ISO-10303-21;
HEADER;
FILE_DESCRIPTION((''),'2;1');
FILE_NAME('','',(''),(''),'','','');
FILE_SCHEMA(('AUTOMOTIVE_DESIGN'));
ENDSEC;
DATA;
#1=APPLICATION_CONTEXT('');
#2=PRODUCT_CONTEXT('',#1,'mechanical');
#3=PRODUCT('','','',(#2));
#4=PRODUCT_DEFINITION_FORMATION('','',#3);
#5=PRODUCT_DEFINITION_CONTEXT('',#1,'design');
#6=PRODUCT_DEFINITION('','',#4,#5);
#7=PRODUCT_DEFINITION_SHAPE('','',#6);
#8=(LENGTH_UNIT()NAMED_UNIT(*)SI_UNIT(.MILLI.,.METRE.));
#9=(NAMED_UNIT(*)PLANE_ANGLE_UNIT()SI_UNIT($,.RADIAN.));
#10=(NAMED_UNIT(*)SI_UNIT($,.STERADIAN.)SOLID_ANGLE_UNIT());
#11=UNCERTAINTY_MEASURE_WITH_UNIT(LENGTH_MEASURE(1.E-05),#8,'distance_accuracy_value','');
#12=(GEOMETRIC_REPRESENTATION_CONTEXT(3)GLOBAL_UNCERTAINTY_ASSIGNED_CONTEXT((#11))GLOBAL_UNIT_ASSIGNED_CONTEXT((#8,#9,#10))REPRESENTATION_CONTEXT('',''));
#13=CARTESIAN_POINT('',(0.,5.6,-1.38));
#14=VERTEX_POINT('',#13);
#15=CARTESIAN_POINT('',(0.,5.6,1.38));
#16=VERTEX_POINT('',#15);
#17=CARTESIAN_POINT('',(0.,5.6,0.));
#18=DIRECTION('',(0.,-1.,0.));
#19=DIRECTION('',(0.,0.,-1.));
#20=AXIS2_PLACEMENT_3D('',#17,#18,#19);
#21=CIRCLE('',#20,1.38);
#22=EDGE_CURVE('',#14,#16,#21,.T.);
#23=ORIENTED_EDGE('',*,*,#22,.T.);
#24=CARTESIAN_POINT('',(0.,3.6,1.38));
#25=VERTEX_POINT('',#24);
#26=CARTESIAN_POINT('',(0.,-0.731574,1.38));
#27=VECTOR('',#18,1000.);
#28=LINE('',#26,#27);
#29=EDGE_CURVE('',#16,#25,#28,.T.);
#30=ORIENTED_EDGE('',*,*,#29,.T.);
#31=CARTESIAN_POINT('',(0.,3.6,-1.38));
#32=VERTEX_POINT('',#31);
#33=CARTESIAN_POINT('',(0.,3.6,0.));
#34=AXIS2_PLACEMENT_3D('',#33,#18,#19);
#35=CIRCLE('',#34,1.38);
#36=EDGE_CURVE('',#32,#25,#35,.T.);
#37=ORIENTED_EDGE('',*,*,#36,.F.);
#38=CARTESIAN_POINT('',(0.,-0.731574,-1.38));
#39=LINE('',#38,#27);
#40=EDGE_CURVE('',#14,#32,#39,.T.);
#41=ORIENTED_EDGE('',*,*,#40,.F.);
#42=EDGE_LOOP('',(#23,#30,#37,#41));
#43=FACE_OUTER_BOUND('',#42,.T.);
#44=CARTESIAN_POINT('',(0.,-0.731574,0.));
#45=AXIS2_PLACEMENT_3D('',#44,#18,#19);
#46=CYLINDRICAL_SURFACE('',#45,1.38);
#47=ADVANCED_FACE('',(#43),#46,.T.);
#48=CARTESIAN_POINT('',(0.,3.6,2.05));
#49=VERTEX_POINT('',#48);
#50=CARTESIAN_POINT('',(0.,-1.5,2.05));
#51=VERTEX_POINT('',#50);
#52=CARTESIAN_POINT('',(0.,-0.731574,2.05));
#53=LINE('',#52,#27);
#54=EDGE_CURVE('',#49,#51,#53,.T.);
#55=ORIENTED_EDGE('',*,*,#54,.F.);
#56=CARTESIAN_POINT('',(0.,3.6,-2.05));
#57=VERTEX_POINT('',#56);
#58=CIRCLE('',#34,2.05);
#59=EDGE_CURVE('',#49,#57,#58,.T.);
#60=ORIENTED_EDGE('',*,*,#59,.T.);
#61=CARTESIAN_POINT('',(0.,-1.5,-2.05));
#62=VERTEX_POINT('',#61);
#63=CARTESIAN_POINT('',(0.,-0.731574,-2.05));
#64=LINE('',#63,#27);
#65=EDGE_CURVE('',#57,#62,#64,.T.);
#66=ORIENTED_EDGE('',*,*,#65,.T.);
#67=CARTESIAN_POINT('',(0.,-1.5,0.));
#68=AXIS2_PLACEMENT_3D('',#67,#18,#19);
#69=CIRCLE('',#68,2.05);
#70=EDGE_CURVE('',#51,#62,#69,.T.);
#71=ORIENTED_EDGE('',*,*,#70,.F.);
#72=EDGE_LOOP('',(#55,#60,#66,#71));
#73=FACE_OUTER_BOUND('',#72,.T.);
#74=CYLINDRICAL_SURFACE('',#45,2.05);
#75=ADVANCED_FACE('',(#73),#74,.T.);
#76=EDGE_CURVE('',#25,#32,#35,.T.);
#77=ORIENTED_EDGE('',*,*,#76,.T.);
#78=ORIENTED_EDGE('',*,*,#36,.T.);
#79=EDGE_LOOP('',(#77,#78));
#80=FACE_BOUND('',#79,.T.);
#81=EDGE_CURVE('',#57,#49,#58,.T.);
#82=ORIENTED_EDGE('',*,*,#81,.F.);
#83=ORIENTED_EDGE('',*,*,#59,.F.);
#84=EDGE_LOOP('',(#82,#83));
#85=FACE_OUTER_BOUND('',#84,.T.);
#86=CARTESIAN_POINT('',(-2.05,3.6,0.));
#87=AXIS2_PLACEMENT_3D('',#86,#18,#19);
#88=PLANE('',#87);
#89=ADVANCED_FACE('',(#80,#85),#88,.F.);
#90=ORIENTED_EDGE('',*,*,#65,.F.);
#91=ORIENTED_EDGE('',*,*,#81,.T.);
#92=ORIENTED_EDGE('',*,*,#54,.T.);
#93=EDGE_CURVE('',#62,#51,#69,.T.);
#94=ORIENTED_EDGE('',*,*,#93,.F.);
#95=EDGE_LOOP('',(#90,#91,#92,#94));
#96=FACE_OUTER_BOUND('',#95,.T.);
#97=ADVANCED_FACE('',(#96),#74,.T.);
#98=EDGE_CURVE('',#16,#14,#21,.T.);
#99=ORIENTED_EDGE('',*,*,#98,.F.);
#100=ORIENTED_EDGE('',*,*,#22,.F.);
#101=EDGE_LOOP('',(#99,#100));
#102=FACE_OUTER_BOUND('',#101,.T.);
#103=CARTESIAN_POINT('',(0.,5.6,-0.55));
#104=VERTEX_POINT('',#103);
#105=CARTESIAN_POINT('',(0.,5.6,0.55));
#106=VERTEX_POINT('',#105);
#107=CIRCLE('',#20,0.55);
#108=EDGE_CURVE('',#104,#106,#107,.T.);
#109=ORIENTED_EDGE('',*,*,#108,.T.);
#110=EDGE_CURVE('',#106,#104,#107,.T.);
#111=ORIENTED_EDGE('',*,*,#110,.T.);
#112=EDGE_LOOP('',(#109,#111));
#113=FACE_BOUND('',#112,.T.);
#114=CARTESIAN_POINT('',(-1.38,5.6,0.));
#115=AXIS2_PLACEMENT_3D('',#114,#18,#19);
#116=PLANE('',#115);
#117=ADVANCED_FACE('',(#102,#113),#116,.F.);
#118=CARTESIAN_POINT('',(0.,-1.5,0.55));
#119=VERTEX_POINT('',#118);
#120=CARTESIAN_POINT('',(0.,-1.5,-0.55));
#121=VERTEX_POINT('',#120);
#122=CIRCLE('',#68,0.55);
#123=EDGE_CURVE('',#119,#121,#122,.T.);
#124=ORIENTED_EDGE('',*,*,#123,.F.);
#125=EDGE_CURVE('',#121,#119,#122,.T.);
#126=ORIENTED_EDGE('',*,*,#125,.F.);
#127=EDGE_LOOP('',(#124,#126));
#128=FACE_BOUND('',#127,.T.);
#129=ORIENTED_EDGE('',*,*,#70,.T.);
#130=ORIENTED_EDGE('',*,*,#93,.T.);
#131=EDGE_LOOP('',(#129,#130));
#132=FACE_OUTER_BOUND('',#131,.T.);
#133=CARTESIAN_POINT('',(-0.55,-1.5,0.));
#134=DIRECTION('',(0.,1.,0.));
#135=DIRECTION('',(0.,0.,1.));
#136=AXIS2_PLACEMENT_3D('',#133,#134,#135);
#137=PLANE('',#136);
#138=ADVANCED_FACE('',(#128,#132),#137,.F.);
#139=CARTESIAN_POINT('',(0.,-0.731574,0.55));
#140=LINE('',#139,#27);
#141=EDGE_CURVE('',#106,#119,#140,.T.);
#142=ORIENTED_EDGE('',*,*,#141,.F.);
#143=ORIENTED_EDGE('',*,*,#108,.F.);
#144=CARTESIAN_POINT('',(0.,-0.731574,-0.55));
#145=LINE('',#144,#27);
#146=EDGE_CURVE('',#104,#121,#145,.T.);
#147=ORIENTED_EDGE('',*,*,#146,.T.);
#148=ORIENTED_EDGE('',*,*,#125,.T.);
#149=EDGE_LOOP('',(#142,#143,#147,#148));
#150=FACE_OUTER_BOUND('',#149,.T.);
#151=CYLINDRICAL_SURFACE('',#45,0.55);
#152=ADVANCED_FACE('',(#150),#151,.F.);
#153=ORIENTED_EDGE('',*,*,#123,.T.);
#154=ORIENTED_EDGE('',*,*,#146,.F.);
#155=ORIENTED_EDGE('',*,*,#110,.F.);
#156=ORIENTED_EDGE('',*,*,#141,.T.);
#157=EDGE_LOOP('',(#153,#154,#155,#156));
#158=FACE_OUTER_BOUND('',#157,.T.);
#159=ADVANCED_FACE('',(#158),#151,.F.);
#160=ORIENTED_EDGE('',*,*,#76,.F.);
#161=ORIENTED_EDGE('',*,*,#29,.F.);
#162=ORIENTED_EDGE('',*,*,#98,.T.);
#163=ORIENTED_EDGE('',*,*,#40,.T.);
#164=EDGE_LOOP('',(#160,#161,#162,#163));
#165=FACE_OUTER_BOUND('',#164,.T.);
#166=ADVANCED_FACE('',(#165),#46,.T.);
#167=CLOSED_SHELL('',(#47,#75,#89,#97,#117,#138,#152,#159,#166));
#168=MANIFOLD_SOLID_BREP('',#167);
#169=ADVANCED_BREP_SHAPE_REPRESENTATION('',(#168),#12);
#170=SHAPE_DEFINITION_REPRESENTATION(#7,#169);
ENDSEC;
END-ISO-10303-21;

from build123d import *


with BuildPart() as part:
    # Sketch1 → Revolve1 (revolve)
    with BuildSketch(Plane.XY, mode=Mode.PRIVATE) as revolve1_sk:
        Polygon((-0.55, -1.5), (-2.05, -1.5), (-2.05, 3.6), (-1.38, 3.6), (-1.38, 5.6), (-0.55, 5.6), align=None)
    revolve(revolve1_sk.sketch.rotate(Axis((0, -0.731574036, 0), (0, 1, 0)), 270), axis=Axis((0, -0.731574036, 0), (0, 1, 0)))


solid = part.part
